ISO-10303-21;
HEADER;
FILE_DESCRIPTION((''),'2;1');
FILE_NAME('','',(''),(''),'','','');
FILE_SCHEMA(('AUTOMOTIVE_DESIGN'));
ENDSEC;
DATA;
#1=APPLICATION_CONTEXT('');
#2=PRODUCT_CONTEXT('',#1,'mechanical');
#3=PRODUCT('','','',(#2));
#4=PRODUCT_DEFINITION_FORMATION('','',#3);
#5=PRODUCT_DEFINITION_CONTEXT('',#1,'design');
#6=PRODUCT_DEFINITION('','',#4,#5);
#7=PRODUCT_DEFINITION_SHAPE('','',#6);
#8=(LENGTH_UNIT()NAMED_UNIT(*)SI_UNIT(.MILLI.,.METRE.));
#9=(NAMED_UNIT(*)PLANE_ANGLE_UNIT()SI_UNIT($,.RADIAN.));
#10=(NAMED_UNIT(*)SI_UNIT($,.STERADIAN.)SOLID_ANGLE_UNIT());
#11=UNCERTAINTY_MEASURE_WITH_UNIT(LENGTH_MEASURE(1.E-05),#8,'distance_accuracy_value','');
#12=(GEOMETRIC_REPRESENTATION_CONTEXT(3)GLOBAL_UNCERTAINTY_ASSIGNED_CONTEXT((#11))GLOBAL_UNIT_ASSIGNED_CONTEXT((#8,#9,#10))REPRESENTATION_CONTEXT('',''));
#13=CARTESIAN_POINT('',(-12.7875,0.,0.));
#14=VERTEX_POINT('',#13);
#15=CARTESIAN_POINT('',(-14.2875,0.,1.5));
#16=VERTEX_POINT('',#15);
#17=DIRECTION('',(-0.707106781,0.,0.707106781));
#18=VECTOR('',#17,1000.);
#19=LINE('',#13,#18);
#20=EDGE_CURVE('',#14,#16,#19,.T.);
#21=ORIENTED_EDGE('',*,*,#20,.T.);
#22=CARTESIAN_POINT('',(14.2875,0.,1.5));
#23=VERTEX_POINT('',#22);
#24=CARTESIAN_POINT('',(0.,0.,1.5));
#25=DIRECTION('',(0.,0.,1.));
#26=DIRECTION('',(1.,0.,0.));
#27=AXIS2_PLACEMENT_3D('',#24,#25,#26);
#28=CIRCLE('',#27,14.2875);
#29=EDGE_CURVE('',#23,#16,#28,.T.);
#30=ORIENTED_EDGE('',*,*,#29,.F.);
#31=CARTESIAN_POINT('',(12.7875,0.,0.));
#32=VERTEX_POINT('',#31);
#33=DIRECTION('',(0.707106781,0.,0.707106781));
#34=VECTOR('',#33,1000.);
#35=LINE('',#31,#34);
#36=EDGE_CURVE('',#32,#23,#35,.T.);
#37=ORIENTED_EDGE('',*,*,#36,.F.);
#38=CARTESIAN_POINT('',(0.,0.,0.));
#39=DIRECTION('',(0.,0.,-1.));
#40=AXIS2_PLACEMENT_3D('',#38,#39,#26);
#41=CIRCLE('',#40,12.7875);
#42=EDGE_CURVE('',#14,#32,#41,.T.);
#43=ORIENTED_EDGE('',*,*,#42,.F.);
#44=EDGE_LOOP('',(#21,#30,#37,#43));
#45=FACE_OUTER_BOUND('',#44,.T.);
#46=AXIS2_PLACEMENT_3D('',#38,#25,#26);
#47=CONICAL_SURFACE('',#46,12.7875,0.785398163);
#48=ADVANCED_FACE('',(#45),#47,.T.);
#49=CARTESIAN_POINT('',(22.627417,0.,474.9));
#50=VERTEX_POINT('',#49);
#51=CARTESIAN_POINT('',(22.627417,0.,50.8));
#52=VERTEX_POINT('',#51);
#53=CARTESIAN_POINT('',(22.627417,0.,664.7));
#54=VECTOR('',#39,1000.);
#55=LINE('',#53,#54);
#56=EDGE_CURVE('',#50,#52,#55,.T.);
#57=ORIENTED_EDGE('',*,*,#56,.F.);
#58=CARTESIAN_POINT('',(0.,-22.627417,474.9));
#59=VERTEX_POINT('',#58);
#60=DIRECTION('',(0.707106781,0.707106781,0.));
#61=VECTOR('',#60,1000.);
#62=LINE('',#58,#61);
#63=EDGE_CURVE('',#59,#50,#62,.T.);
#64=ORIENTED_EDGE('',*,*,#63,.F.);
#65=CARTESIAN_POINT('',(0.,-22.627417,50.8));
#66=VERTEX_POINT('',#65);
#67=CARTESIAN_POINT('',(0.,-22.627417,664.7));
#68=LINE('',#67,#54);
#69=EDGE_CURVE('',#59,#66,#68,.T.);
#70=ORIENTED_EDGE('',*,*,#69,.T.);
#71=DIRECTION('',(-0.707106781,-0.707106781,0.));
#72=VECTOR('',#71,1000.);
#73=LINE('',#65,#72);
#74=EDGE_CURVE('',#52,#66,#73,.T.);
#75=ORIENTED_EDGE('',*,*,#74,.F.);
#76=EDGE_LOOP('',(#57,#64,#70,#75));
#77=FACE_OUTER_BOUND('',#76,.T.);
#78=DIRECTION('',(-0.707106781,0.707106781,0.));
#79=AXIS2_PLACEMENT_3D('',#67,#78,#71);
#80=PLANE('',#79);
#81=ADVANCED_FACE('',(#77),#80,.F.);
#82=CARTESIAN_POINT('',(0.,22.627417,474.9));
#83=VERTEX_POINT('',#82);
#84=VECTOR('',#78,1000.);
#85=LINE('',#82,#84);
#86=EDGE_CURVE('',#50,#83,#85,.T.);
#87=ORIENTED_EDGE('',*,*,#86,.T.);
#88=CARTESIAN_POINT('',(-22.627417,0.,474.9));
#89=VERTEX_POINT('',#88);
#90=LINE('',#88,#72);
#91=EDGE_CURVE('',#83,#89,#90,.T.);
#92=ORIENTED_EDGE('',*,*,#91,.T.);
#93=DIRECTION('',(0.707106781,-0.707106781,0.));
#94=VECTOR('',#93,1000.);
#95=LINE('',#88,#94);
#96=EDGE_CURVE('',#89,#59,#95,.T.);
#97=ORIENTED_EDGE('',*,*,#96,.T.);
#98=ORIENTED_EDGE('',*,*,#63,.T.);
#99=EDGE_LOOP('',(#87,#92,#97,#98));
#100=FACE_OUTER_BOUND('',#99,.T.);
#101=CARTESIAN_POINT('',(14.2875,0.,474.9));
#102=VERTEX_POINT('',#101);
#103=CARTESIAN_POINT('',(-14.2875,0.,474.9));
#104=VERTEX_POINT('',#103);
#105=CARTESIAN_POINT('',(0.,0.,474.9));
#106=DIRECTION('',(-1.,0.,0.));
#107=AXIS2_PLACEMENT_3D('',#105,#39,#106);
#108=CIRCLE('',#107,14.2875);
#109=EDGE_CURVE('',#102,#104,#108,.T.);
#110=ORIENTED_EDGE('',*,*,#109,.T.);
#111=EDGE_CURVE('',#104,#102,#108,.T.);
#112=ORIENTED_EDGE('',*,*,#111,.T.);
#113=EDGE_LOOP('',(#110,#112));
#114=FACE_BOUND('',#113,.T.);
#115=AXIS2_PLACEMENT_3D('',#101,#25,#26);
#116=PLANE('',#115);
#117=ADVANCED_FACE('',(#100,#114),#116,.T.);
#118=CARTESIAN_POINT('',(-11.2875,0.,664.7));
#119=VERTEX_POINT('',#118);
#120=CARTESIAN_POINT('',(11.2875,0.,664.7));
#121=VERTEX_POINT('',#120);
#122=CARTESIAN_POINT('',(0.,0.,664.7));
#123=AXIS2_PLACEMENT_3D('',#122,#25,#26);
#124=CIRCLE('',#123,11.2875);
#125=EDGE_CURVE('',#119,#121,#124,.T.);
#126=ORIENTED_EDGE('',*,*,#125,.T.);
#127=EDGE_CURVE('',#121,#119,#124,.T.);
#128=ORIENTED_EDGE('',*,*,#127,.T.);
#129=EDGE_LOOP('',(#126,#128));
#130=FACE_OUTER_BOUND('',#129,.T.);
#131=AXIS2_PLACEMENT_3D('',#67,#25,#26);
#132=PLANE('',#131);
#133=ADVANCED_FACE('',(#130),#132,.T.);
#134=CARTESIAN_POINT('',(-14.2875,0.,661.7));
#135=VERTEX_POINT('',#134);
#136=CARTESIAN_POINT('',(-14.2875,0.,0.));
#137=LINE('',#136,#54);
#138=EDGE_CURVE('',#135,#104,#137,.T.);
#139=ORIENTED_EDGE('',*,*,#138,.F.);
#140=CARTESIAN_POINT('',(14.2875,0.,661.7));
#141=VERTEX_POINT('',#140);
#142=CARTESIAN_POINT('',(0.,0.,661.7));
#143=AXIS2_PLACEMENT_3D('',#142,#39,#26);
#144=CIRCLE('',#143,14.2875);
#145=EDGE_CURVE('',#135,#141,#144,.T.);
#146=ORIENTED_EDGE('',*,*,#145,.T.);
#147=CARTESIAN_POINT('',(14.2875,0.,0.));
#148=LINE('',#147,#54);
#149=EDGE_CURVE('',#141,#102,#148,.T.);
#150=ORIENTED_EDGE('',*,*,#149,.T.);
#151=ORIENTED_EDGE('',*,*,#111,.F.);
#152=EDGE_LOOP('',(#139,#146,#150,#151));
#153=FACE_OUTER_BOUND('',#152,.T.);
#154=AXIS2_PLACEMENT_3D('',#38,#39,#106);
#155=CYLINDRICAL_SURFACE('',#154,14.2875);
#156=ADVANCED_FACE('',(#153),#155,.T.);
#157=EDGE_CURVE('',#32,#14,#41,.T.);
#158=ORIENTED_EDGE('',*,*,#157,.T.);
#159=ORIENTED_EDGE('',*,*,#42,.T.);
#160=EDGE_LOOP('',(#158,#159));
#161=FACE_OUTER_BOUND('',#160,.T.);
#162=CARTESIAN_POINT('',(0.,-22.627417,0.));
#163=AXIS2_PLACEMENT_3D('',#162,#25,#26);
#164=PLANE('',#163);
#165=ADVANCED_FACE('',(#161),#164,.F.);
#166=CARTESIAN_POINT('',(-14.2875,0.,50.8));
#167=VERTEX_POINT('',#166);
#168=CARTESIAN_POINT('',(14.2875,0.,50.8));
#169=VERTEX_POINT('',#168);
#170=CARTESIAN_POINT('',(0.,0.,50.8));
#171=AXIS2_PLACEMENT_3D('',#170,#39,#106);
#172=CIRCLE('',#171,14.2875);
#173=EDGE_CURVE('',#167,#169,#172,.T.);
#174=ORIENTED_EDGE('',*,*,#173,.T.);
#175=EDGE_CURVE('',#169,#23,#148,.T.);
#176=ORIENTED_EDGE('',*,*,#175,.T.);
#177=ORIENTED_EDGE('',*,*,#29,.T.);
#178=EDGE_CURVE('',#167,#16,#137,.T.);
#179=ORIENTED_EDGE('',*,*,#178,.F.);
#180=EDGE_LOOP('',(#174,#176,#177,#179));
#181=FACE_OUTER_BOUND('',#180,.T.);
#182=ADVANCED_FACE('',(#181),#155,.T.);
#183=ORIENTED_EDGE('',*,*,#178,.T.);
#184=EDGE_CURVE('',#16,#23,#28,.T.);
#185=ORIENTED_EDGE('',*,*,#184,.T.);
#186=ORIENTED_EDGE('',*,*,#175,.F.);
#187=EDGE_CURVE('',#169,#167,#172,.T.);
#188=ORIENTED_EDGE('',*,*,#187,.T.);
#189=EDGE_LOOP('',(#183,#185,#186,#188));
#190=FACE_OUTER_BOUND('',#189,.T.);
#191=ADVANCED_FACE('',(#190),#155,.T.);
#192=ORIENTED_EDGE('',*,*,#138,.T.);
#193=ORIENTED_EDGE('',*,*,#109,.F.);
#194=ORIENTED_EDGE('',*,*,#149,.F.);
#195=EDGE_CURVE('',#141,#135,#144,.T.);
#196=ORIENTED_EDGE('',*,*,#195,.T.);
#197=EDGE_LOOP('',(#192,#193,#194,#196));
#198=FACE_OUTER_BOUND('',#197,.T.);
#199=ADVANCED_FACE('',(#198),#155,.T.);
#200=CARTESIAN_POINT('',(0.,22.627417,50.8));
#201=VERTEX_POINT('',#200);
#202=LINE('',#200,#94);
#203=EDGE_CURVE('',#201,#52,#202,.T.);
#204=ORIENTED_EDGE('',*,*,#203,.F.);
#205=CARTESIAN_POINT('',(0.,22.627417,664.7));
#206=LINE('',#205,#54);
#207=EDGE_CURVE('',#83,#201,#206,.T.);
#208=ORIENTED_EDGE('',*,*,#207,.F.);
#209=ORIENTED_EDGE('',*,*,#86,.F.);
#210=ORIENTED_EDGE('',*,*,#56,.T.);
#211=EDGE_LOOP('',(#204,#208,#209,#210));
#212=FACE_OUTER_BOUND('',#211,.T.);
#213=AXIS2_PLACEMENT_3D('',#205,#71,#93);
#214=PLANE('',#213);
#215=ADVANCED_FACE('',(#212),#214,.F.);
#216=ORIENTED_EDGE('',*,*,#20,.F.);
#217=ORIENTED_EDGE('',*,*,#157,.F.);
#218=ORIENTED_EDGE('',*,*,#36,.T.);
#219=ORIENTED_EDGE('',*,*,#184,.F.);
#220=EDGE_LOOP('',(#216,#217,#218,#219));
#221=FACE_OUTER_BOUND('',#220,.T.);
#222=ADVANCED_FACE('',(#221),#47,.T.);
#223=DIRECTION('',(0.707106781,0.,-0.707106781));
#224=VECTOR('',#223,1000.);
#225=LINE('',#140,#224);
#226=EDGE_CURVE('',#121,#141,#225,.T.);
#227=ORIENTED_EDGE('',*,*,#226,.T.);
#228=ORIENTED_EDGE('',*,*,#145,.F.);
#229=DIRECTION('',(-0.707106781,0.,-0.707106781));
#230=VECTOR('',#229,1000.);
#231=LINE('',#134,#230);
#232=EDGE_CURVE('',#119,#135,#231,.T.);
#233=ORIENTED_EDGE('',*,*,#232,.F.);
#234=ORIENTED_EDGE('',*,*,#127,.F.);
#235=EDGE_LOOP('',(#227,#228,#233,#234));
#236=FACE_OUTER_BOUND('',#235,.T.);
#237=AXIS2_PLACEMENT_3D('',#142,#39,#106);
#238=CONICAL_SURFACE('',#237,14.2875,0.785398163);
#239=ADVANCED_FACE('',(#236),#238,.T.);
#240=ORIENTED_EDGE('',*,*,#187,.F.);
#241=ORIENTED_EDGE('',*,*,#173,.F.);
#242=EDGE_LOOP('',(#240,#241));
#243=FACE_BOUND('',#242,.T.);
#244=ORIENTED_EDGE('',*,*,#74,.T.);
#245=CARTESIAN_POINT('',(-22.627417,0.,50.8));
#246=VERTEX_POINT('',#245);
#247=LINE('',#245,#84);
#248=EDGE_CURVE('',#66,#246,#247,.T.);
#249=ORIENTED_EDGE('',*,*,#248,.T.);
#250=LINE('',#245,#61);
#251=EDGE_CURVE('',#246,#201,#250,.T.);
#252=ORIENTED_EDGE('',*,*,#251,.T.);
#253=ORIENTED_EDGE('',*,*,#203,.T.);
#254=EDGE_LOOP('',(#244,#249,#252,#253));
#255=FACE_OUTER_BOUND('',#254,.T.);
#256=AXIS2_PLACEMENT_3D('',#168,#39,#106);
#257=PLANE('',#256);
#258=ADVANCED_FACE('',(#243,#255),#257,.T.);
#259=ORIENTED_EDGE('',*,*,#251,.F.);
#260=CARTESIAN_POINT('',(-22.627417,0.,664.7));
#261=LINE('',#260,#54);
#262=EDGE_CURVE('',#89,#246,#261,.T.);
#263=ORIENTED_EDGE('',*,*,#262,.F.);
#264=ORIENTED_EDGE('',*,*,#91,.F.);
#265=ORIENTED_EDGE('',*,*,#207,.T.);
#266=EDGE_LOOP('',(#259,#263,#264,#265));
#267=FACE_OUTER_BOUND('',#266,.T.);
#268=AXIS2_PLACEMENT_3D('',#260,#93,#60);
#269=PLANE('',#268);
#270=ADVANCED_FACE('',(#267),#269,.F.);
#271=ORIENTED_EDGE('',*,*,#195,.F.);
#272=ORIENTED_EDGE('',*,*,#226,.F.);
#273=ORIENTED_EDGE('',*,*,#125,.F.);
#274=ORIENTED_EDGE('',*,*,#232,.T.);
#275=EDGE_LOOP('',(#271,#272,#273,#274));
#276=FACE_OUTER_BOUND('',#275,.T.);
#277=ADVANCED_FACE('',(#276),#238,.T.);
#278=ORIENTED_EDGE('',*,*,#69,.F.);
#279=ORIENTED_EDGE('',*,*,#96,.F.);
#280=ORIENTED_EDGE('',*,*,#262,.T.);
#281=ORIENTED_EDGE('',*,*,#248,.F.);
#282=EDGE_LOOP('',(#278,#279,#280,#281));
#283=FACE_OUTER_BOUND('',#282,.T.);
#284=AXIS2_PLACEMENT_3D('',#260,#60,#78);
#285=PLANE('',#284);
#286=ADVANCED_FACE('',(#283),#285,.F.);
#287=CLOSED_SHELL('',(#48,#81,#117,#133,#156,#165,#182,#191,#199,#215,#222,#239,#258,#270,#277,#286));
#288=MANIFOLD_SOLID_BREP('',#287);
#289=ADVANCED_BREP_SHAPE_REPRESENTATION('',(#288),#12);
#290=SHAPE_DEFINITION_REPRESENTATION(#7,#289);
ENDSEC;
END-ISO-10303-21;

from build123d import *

# Parameters (mm, degrees)
EXTRUDE1_DEPTH = 664.7
SKETCH2_W      = 10
SKETCH2_H      = 50.8
SKETCH2_H_2    = 189.8
CHAMFER1_SIZE  = 1.5
CHAMFER2_SIZE  = 3


with BuildPart() as part:
    # Sketch1 → Extrude1 (new body)
    with BuildSketch(Plane.XY):
        Polygon((-22.627416998, 0), (0, 22.627416998), (22.627416998, 0), (0, -22.627416998), align=None)
    extrude(amount=EXTRUDE1_DEPTH)

    # Sketch2 → Cut-Revolve1 (revolve, cut)
    with BuildSketch(Plane(origin=(0, 0, 0), x_dir=(1, 0, 0), z_dir=(0, 1, 0)), mode=Mode.PRIVATE) as cut_revolve1_sk:
        with Locations((19.2875, -25.4)):
            Rectangle(SKETCH2_W, SKETCH2_H)
        with Locations((19.2875, -569.8)):
            Rectangle(SKETCH2_W, SKETCH2_H_2)
    revolve(cut_revolve1_sk.sketch.rotate(Axis((0, 0, 0), (0, 0, 1)), 180), axis=Axis((0, 0, 0), (0, 0, 1)), mode=Mode.SUBTRACT)

    # Chamfer1
    chamfer1_edges = [part.edges().sort_by_distance(p)[0] for p in [
        (14.2875, 0, 0),
    ]]
    chamfer(chamfer1_edges, length=CHAMFER1_SIZE)

    # Chamfer2
    chamfer2_edges = [part.edges().sort_by_distance(p)[0] for p in [
        (14.2875, 0, 664.7),
    ]]
    chamfer(chamfer2_edges, length=CHAMFER2_SIZE)


solid = part.part
